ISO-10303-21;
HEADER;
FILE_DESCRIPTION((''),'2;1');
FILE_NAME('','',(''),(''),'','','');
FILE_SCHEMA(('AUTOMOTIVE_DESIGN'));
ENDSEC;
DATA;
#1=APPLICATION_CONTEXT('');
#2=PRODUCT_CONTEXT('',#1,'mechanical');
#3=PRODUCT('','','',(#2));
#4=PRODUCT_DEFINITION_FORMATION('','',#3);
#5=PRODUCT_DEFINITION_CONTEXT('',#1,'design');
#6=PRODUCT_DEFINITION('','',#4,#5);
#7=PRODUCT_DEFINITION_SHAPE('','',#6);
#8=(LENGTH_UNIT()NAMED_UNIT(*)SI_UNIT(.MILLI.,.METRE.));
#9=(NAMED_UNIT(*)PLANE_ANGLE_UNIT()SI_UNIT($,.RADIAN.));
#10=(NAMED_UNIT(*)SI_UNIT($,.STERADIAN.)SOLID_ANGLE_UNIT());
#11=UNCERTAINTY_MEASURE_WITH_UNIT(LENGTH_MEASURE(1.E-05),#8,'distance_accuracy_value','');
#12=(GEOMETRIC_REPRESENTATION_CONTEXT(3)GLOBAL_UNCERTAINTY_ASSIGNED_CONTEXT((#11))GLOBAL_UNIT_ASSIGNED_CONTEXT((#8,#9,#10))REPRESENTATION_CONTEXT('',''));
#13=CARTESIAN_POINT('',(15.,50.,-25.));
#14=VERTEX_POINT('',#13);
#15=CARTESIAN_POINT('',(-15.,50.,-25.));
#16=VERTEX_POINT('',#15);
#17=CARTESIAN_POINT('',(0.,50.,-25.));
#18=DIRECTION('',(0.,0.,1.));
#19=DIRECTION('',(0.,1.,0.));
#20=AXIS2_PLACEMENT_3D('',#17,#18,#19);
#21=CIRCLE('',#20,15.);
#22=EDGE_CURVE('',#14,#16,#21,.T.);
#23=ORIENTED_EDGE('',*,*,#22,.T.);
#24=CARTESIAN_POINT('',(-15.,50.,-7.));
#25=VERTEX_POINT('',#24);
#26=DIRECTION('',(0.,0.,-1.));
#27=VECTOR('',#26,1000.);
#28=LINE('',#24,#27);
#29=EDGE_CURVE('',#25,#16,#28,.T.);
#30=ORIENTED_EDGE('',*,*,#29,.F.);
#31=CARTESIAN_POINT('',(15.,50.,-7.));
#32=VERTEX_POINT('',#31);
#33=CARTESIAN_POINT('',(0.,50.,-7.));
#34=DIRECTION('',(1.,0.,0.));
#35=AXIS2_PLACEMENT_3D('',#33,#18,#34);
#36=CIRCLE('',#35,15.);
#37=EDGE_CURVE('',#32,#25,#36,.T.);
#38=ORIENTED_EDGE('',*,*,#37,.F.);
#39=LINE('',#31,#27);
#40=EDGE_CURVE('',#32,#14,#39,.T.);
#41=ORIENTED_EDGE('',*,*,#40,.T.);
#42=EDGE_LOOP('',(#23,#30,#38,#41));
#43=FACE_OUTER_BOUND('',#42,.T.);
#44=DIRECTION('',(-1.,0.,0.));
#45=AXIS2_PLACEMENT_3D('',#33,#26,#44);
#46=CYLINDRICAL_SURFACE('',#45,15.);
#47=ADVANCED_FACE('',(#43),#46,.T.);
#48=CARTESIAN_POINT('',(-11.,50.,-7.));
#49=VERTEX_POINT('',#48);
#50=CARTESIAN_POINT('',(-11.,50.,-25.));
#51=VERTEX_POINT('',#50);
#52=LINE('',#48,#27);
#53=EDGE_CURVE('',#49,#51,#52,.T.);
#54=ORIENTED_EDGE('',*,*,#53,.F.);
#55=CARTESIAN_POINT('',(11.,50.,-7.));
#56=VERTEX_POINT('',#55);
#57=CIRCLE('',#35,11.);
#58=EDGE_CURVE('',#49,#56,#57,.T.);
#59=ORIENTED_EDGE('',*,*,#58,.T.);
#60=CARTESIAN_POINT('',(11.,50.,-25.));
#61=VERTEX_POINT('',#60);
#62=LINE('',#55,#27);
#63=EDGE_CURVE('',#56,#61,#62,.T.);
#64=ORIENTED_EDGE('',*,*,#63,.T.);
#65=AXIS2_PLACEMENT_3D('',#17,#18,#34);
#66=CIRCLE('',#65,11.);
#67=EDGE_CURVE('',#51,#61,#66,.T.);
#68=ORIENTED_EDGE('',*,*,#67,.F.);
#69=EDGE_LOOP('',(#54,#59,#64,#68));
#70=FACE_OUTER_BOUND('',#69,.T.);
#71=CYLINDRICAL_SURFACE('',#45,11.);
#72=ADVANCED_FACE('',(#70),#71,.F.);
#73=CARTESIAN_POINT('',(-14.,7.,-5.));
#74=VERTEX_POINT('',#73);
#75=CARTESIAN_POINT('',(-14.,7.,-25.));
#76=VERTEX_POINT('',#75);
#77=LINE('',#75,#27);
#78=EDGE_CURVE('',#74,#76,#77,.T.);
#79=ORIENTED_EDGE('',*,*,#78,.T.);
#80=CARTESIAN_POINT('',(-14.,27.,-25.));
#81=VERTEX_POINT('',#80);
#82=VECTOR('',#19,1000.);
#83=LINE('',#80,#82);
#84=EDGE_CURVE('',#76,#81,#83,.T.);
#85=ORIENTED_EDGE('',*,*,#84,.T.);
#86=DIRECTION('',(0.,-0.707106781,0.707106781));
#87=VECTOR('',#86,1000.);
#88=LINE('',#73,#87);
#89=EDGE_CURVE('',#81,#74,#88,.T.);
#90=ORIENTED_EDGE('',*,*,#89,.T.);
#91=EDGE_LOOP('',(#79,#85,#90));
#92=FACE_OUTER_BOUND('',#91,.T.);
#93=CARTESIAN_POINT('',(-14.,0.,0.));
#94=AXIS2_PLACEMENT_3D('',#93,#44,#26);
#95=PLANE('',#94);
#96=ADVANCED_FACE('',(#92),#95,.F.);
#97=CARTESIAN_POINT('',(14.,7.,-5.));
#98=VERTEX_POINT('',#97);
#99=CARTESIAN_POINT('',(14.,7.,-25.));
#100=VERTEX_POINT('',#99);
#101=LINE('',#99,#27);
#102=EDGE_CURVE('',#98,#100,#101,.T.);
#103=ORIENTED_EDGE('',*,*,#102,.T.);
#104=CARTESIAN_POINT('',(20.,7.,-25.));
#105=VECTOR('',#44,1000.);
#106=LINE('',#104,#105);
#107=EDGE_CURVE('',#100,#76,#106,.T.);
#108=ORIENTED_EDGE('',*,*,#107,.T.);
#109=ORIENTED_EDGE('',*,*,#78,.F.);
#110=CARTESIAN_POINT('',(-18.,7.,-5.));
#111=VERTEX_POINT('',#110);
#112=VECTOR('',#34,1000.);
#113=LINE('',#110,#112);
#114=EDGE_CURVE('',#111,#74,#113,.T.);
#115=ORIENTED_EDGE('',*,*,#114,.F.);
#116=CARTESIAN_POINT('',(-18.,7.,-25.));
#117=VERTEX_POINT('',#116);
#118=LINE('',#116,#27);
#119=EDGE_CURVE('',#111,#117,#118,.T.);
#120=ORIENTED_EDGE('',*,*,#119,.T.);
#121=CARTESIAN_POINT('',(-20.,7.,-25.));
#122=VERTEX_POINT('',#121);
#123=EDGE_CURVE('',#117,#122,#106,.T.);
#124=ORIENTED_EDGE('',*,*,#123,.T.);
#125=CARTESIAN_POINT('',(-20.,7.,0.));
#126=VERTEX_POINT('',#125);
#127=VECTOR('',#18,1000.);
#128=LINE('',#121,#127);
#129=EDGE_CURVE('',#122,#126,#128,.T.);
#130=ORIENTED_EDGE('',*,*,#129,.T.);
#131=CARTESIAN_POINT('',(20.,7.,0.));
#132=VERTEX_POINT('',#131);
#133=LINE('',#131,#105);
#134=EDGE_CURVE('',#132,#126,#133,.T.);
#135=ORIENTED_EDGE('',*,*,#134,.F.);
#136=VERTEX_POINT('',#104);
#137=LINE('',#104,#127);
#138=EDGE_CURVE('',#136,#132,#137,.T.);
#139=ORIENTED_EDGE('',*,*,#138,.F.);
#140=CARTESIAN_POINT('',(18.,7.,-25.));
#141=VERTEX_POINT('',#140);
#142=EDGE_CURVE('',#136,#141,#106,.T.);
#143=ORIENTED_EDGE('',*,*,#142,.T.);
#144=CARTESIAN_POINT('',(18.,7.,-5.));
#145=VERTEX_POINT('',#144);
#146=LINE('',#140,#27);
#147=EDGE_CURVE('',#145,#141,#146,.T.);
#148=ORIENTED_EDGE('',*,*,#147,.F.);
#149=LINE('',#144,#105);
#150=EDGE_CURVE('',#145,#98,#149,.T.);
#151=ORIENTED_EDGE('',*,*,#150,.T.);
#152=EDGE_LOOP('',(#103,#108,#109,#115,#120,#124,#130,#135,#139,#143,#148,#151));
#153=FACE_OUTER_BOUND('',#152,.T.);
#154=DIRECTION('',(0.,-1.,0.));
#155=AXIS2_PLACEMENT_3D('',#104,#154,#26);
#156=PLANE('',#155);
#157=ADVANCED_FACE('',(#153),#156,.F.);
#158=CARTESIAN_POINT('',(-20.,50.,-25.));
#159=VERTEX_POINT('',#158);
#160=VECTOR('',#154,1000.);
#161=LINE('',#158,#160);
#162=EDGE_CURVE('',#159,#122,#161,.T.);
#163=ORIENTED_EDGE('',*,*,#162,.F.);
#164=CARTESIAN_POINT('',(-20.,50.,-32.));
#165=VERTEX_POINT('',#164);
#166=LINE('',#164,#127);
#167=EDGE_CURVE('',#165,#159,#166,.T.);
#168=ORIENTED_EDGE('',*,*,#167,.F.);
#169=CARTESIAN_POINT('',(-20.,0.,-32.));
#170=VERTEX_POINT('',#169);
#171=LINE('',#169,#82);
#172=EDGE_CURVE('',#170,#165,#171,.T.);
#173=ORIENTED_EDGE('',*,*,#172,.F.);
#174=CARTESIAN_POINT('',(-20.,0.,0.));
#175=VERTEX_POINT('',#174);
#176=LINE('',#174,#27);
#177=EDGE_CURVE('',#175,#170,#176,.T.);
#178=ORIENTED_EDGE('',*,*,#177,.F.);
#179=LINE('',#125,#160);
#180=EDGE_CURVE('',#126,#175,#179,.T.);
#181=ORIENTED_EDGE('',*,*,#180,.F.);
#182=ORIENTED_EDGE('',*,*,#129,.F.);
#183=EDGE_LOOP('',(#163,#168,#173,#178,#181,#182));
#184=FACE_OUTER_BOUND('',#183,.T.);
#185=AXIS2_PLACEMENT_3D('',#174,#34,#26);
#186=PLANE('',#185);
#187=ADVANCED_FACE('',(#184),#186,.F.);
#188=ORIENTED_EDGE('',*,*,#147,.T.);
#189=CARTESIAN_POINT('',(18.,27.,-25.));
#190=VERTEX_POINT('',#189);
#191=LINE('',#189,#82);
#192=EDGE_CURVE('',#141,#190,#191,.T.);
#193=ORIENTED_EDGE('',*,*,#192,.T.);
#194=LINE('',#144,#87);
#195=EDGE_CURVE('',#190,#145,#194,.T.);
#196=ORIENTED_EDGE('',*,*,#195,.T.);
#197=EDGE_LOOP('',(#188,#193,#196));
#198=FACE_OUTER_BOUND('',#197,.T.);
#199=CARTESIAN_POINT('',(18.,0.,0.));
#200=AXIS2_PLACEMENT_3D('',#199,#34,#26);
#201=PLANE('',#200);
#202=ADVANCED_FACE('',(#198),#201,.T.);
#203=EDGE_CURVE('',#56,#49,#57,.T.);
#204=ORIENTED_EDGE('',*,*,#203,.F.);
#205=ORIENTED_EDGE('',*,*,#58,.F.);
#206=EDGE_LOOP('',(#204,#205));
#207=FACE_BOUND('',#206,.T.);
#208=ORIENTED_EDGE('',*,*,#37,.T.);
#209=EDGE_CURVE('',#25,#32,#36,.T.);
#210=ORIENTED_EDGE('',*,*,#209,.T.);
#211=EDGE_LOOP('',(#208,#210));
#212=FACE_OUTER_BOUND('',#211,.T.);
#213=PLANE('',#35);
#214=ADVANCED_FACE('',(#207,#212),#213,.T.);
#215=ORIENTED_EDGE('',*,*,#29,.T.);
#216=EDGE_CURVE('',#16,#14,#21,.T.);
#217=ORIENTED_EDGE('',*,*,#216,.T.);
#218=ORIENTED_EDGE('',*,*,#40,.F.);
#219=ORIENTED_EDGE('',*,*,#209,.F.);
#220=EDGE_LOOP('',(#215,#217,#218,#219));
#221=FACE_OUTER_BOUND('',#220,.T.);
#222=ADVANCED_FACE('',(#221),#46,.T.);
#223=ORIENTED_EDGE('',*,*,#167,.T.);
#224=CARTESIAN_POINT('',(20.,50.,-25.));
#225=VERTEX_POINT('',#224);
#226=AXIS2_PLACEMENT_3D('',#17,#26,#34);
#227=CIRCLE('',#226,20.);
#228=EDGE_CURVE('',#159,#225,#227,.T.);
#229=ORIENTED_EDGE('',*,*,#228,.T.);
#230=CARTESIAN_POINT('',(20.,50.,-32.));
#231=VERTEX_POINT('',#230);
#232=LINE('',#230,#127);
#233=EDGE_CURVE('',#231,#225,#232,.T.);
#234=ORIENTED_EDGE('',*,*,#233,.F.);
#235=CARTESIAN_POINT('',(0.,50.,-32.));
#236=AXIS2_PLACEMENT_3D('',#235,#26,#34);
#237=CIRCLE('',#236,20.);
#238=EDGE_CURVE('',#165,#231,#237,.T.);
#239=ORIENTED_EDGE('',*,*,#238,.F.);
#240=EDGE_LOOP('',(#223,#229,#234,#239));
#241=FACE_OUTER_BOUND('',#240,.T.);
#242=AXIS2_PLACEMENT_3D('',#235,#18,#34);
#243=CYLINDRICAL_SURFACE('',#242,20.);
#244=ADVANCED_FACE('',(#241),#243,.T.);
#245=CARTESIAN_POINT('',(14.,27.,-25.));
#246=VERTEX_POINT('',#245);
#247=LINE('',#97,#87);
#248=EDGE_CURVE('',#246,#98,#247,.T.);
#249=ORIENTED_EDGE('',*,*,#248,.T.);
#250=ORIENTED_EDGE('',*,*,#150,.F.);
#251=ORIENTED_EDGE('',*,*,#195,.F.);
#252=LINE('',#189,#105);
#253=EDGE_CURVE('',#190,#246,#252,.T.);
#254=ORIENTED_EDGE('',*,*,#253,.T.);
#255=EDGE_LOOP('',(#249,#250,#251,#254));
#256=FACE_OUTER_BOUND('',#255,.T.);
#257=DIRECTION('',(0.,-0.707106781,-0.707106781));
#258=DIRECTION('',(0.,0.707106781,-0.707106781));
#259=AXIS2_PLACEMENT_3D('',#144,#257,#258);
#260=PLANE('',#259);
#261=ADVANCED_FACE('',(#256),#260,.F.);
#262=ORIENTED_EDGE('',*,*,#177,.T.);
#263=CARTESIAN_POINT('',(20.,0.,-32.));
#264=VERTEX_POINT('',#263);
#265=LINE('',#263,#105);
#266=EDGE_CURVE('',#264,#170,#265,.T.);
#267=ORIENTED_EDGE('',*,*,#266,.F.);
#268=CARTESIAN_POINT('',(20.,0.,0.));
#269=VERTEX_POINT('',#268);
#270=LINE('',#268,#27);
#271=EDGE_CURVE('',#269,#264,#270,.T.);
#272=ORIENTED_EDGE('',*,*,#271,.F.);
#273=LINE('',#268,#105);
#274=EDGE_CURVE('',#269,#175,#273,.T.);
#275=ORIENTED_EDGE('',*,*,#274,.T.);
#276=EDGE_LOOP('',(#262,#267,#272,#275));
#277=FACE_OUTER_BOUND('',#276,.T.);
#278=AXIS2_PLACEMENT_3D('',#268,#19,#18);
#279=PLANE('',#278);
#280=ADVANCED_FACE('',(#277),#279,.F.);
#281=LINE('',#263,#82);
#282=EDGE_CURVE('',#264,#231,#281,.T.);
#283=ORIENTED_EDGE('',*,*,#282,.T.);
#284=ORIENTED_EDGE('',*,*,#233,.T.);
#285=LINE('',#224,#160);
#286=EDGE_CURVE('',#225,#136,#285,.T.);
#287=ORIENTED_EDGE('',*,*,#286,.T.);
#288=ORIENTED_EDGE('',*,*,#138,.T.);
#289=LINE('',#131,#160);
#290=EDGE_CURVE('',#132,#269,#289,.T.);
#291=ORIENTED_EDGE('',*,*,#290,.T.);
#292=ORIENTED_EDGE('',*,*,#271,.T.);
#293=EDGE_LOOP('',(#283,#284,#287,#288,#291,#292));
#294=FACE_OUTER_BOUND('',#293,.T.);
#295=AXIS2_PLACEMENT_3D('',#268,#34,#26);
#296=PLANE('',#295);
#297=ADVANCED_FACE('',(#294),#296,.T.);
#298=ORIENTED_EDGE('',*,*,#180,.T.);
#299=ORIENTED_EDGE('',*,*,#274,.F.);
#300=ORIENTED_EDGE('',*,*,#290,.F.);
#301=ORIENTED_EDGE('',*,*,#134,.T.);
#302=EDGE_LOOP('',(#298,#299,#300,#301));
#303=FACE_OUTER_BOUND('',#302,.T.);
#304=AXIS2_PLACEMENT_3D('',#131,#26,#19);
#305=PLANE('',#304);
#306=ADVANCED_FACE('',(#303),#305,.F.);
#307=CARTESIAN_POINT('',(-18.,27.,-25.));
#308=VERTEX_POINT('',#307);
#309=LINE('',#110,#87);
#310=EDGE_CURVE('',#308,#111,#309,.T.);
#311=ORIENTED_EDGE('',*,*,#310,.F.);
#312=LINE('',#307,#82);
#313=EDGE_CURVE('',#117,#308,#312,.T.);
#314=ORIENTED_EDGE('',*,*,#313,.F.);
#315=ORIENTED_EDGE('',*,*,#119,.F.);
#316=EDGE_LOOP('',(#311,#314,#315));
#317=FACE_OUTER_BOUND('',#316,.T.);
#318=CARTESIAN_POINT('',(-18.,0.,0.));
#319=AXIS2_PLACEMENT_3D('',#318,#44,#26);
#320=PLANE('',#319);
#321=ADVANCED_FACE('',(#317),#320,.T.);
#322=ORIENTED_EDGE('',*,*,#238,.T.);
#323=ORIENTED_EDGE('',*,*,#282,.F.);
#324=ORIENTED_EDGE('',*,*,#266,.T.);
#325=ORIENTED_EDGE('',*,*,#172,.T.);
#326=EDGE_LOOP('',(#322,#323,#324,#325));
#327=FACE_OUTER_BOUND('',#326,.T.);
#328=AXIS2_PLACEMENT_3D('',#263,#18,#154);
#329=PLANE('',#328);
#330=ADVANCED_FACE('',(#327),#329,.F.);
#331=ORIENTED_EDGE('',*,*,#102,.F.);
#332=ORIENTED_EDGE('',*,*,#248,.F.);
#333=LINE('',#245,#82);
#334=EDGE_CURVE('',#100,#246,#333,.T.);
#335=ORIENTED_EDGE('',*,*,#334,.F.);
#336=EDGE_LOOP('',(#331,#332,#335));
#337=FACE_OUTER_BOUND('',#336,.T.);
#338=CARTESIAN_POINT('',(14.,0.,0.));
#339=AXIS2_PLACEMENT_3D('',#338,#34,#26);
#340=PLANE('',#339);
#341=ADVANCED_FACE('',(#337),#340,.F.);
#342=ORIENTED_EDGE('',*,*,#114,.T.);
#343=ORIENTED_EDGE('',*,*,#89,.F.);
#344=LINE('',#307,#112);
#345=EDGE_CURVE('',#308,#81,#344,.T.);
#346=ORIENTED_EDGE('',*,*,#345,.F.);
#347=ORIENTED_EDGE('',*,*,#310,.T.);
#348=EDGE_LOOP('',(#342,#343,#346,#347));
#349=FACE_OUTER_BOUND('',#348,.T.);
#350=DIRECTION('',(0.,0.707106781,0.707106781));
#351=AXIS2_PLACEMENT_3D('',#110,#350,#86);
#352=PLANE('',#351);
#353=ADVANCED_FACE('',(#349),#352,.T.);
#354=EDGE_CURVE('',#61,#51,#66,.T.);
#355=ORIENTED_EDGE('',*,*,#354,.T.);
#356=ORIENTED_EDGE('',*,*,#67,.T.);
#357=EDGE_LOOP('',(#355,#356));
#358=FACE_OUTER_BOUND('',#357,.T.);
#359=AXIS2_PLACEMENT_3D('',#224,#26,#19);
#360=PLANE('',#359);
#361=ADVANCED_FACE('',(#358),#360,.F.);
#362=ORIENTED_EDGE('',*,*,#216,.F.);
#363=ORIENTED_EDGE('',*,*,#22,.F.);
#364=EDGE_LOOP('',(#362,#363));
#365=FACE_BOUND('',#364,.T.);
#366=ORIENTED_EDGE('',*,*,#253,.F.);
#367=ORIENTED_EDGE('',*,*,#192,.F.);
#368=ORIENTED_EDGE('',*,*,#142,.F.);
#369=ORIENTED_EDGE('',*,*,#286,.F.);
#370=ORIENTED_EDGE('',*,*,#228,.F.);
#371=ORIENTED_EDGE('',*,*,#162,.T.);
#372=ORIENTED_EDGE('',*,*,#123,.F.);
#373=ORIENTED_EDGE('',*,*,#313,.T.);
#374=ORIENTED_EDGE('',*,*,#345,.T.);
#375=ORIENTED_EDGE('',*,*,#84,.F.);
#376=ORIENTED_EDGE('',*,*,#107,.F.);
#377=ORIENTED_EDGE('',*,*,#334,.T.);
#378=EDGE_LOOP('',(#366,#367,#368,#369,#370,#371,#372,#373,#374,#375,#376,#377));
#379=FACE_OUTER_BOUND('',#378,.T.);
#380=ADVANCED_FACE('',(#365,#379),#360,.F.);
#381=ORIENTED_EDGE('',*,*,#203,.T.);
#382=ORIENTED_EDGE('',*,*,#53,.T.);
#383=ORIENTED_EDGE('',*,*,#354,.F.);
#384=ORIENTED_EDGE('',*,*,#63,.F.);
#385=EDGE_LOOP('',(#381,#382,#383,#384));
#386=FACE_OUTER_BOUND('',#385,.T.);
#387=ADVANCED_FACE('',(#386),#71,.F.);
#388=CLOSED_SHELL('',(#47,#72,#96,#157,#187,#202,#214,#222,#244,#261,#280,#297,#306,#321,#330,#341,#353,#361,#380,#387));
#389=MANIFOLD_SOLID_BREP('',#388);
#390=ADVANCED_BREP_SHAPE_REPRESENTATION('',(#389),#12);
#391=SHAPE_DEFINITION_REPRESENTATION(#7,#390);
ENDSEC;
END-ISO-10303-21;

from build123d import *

# Parameters (mm, degrees)
BASE_ANGLE_DEPTH             = 20
UPRIGHT_PLATE_SKETCH_W       = 40
UPRIGHT_PLATE_SKETCH_H       = 43
UPRIGHT_PLATE_DEPTH          = 7
BEARING_HUB_SKETCH_R         = 15
BEARING_HUB_SKETCH_R_2       = 11
BEARING_HUB_30_BORE_22_DEPTH = 18
GUSSET_START                 = -6
GUSSET_RIB_DEPTH             = 4


with BuildPart() as part:
    # Base Angle Profile Sketch → Base Angle (new, symmetric)
    with BuildSketch(Plane(origin=(0, 0, 0), x_dir=(0, 0, -1), z_dir=(1, 0, 0))):
        Polygon((0, 0), (32, 0), (32, 50), (25, 50), (25, 7), (0, 7), align=None)
    extrude(amount=BASE_ANGLE_DEPTH, both=True)

    # Upright Plate Sketch → Upright Plate (add)
    with BuildSketch(Plane.XY.offset(-25)):
        with Locations((0, 28.5)):
            Rectangle(UPRIGHT_PLATE_SKETCH_W, UPRIGHT_PLATE_SKETCH_H)
        with BuildLine():
            ThreePointArc((20, 50), (0, 70), (-20, 50))
            Line((-20, 50), (20, 50))
        make_face()
    extrude(amount=-UPRIGHT_PLATE_DEPTH)

    # Bearing Hub Sketch → Bearing Hub Ø30 Bore Ø22 (add)
    with BuildSketch(Plane.XY.offset(-25)):
        with Locations(Location((0, 50, 0), (0, 0, 90))):
            Circle(BEARING_HUB_SKETCH_R)
        with Locations((0, 50)):
            Circle(BEARING_HUB_SKETCH_R_2, mode=Mode.SUBTRACT)
    extrude(amount=BEARING_HUB_30_BORE_22_DEPTH)

    # Gusset Rib Sketch → Gusset Rib (add)
    with BuildSketch(Plane(origin=(20, 0, 0), x_dir=(0, 0, -1), z_dir=(1, 0, 0)).offset(GUSSET_START)):
        Polygon((5, 7), (25, 27), (25, 7), align=None)
    gusset_rib = extrude(amount=GUSSET_RIB_DEPTH)

    # Gusset Rib Mirror: Gusset Rib across plane
    add(gusset_rib.mirror(Plane(origin=(0, 0, 0), x_dir=(0, 0, 1), z_dir=(1, 0, 0))))


solid = part.part
